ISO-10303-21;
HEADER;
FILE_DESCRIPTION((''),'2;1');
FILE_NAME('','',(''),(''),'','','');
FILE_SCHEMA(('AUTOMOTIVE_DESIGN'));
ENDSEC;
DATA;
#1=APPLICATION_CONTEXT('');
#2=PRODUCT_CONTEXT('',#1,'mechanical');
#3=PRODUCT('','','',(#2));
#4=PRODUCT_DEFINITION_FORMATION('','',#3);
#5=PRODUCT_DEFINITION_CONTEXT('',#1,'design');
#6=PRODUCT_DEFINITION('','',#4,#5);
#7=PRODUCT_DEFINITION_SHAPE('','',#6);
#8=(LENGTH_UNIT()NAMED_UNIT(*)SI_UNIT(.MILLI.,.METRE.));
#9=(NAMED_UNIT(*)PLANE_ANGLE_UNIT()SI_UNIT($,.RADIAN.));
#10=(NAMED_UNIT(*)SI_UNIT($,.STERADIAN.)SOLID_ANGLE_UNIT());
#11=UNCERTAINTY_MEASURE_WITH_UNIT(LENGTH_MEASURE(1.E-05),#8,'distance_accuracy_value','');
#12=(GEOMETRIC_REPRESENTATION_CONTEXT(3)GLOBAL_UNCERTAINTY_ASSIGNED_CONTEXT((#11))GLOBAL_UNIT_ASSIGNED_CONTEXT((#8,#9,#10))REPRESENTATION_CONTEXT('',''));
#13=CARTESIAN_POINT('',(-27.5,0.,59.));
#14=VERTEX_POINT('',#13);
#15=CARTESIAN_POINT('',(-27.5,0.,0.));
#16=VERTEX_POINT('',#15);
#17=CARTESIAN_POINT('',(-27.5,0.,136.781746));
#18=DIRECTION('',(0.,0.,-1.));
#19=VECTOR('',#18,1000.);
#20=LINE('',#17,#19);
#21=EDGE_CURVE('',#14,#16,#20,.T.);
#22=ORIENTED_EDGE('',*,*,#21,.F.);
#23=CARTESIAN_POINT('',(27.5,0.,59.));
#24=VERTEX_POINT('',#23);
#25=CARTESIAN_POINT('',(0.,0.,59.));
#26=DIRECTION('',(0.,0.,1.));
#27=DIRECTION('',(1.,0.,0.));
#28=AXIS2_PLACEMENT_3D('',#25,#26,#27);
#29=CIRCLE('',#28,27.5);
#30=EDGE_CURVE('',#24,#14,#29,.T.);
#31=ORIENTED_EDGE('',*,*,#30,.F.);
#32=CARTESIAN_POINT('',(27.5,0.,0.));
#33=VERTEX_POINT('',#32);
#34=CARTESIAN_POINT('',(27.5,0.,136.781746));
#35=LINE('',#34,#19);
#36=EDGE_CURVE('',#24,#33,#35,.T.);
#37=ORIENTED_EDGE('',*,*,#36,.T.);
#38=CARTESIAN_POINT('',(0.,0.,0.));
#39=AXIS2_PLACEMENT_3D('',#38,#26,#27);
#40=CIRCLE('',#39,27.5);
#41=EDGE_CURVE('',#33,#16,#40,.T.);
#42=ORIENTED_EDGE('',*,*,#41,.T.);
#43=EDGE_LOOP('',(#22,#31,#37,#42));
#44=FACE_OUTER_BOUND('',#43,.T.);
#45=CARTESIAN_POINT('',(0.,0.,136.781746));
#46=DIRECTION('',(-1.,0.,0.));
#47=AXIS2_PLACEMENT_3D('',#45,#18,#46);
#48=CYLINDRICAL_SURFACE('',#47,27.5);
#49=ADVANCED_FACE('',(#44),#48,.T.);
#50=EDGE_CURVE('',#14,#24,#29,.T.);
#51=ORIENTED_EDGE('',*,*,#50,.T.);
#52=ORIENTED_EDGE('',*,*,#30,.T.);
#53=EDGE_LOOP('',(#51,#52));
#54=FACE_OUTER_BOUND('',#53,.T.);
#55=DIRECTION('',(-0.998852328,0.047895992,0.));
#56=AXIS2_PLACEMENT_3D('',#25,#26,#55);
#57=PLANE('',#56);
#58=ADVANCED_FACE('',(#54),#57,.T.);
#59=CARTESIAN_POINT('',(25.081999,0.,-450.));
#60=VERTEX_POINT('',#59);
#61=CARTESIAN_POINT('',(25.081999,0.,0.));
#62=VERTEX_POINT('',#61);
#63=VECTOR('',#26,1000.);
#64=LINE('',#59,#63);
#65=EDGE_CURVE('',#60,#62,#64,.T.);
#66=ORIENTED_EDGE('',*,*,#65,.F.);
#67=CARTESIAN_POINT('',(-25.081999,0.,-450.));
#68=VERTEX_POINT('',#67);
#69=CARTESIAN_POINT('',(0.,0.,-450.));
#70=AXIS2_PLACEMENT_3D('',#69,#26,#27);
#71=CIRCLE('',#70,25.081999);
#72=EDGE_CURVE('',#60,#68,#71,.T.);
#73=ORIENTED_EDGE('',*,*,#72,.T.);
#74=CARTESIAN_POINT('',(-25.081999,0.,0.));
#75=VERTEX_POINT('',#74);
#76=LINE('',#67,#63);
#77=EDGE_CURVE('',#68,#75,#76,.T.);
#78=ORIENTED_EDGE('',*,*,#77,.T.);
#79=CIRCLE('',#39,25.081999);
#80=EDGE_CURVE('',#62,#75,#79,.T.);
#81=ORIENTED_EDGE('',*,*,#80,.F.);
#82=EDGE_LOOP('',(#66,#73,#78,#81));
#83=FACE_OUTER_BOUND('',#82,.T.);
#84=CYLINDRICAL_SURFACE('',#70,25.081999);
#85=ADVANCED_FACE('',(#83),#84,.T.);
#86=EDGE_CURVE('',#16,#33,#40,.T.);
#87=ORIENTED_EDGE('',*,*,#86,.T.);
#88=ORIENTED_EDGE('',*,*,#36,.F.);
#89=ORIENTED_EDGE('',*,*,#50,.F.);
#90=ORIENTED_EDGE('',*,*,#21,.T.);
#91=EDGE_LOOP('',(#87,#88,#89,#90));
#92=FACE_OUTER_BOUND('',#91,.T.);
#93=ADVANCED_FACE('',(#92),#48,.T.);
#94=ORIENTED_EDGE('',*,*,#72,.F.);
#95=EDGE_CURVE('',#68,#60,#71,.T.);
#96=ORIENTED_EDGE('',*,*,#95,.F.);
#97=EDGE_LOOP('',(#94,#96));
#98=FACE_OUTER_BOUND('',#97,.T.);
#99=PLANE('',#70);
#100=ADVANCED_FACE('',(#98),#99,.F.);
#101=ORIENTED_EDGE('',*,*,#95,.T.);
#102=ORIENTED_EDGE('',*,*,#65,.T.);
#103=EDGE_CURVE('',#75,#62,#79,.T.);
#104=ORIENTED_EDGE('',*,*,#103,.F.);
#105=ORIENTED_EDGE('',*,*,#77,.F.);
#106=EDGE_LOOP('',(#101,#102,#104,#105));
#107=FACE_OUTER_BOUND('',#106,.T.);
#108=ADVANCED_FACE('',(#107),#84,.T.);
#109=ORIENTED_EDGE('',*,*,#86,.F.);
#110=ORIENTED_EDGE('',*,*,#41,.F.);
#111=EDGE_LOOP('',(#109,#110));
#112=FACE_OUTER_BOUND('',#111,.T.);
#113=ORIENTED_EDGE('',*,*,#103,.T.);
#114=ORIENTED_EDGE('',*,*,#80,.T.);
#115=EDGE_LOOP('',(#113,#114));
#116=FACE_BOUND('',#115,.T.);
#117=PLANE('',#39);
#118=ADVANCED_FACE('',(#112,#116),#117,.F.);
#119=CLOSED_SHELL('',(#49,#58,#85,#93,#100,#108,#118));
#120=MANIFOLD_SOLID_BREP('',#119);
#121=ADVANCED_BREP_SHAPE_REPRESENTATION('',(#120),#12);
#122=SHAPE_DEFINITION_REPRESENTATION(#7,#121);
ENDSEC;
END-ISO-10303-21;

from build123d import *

# Parameters (mm, degrees)
SKETCH1_R           = 25.081999049
BOSS_EXTRUDE1_DEPTH = 450
SKETCH2_R           = 27.5
BOSS_EXTRUDE2_DEPTH = 59


with BuildPart() as part:
    # Sketch1 → Boss-Extrude1 (new body)
    with BuildSketch(Plane.XY):
        Circle(SKETCH1_R)
    extrude(amount=-BOSS_EXTRUDE1_DEPTH)

    # Sketch2 → Boss-Extrude2 (add)
    with BuildSketch(Plane.XY):
        Circle(SKETCH2_R)
    extrude(amount=BOSS_EXTRUDE2_DEPTH)


solid = part.part
